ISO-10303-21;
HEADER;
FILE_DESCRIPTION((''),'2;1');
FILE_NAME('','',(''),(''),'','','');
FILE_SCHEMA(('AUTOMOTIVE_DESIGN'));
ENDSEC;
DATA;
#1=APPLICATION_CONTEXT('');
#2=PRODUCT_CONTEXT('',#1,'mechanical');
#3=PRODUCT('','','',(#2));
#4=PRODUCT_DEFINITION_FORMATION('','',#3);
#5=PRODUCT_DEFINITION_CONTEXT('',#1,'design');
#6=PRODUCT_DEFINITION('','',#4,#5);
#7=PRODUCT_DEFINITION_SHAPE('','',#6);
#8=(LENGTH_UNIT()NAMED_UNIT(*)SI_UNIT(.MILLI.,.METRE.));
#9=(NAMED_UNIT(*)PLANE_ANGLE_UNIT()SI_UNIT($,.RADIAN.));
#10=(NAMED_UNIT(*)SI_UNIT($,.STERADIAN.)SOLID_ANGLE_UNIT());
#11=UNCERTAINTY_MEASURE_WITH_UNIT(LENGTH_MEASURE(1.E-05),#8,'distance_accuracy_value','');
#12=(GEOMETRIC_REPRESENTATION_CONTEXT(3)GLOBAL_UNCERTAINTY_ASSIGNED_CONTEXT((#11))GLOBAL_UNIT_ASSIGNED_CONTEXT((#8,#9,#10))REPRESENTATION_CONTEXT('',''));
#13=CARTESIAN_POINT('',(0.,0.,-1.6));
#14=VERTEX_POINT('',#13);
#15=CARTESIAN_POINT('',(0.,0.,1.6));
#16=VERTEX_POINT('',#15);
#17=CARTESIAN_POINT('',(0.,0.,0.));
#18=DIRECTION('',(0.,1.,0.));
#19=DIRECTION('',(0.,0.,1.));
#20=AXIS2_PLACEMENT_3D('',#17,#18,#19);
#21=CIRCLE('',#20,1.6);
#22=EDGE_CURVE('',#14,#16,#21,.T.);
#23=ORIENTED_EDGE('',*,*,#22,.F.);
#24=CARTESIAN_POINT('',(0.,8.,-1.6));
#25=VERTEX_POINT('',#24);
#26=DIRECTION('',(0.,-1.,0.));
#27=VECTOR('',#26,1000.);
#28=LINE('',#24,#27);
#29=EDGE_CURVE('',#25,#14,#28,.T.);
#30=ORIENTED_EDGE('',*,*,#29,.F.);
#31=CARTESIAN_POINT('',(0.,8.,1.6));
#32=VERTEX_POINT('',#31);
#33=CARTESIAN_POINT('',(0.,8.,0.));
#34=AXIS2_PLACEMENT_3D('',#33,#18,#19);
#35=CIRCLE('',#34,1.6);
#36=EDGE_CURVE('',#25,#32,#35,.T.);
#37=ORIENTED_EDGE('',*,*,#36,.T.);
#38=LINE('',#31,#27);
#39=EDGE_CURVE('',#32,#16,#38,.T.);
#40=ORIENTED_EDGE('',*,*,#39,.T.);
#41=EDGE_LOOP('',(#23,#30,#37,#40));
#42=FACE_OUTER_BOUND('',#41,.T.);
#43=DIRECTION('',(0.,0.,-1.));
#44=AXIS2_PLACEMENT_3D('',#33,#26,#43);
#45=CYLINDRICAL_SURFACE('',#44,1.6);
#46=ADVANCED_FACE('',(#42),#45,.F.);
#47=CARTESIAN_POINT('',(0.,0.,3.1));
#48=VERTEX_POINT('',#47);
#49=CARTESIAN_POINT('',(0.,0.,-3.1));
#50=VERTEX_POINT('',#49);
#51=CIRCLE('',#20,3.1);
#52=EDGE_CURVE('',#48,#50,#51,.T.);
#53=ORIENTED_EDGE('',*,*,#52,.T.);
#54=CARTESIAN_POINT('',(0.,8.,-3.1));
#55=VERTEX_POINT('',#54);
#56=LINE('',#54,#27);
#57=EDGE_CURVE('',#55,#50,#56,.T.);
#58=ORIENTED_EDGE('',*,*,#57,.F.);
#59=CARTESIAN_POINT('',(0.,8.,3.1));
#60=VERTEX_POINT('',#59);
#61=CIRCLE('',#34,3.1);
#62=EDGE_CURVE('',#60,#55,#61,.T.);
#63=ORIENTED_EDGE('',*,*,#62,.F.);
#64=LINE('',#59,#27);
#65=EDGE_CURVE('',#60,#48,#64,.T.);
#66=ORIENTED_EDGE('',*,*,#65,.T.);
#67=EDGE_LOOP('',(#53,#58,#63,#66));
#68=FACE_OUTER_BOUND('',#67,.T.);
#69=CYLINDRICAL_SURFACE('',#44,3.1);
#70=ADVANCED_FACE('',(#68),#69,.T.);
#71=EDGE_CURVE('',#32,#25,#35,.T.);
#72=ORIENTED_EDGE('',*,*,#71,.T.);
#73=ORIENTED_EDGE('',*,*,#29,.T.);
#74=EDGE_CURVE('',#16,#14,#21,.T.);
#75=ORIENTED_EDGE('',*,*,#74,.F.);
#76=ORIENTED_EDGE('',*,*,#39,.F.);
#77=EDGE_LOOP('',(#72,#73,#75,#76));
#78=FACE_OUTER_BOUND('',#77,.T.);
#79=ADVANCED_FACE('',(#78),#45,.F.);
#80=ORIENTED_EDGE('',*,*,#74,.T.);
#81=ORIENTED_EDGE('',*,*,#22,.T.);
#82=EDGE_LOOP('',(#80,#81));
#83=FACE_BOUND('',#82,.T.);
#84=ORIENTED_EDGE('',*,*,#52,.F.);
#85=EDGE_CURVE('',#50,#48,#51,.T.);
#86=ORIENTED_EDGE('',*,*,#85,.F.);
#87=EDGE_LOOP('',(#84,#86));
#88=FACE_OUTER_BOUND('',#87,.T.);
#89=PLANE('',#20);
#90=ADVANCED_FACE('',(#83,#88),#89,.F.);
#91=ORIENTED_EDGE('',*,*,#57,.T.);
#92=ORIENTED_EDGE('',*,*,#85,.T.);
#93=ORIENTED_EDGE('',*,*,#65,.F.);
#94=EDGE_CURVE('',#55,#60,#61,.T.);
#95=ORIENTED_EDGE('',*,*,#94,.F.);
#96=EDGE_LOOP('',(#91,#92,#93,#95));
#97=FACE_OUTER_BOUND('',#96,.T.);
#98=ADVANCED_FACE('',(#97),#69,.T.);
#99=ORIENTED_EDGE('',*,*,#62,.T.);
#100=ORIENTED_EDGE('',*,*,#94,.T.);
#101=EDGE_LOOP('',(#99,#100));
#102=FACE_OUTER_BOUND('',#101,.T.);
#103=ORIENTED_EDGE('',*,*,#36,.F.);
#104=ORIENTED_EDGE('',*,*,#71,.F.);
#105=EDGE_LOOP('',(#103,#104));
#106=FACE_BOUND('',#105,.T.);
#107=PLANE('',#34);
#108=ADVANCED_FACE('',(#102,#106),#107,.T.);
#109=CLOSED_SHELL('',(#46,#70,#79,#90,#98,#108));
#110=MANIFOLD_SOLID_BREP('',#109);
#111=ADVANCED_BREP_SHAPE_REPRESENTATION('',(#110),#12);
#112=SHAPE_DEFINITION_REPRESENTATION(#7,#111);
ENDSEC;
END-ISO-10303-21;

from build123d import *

# Parameters (mm, degrees)
SKETCH_1_R      = 3.1
SKETCH_1_R_2    = 1.6
EXTRUDE_1_DEPTH = 8


with BuildPart() as part:
    # 草图1 → 凸台-拉伸1 (new body)
    with BuildSketch(Plane(origin=(0, 0, 0), x_dir=(1, 0, 0), z_dir=(0, 1, 0))):
        with Locations(Location((0, 0, 0), (0, 0, 270))):
            Circle(SKETCH_1_R)
        with Locations(Location((0, 0, 0), (0, 0, 270))):
            Circle(SKETCH_1_R_2, mode=Mode.SUBTRACT)
    extrude(amount=EXTRUDE_1_DEPTH)


solid = part.part
